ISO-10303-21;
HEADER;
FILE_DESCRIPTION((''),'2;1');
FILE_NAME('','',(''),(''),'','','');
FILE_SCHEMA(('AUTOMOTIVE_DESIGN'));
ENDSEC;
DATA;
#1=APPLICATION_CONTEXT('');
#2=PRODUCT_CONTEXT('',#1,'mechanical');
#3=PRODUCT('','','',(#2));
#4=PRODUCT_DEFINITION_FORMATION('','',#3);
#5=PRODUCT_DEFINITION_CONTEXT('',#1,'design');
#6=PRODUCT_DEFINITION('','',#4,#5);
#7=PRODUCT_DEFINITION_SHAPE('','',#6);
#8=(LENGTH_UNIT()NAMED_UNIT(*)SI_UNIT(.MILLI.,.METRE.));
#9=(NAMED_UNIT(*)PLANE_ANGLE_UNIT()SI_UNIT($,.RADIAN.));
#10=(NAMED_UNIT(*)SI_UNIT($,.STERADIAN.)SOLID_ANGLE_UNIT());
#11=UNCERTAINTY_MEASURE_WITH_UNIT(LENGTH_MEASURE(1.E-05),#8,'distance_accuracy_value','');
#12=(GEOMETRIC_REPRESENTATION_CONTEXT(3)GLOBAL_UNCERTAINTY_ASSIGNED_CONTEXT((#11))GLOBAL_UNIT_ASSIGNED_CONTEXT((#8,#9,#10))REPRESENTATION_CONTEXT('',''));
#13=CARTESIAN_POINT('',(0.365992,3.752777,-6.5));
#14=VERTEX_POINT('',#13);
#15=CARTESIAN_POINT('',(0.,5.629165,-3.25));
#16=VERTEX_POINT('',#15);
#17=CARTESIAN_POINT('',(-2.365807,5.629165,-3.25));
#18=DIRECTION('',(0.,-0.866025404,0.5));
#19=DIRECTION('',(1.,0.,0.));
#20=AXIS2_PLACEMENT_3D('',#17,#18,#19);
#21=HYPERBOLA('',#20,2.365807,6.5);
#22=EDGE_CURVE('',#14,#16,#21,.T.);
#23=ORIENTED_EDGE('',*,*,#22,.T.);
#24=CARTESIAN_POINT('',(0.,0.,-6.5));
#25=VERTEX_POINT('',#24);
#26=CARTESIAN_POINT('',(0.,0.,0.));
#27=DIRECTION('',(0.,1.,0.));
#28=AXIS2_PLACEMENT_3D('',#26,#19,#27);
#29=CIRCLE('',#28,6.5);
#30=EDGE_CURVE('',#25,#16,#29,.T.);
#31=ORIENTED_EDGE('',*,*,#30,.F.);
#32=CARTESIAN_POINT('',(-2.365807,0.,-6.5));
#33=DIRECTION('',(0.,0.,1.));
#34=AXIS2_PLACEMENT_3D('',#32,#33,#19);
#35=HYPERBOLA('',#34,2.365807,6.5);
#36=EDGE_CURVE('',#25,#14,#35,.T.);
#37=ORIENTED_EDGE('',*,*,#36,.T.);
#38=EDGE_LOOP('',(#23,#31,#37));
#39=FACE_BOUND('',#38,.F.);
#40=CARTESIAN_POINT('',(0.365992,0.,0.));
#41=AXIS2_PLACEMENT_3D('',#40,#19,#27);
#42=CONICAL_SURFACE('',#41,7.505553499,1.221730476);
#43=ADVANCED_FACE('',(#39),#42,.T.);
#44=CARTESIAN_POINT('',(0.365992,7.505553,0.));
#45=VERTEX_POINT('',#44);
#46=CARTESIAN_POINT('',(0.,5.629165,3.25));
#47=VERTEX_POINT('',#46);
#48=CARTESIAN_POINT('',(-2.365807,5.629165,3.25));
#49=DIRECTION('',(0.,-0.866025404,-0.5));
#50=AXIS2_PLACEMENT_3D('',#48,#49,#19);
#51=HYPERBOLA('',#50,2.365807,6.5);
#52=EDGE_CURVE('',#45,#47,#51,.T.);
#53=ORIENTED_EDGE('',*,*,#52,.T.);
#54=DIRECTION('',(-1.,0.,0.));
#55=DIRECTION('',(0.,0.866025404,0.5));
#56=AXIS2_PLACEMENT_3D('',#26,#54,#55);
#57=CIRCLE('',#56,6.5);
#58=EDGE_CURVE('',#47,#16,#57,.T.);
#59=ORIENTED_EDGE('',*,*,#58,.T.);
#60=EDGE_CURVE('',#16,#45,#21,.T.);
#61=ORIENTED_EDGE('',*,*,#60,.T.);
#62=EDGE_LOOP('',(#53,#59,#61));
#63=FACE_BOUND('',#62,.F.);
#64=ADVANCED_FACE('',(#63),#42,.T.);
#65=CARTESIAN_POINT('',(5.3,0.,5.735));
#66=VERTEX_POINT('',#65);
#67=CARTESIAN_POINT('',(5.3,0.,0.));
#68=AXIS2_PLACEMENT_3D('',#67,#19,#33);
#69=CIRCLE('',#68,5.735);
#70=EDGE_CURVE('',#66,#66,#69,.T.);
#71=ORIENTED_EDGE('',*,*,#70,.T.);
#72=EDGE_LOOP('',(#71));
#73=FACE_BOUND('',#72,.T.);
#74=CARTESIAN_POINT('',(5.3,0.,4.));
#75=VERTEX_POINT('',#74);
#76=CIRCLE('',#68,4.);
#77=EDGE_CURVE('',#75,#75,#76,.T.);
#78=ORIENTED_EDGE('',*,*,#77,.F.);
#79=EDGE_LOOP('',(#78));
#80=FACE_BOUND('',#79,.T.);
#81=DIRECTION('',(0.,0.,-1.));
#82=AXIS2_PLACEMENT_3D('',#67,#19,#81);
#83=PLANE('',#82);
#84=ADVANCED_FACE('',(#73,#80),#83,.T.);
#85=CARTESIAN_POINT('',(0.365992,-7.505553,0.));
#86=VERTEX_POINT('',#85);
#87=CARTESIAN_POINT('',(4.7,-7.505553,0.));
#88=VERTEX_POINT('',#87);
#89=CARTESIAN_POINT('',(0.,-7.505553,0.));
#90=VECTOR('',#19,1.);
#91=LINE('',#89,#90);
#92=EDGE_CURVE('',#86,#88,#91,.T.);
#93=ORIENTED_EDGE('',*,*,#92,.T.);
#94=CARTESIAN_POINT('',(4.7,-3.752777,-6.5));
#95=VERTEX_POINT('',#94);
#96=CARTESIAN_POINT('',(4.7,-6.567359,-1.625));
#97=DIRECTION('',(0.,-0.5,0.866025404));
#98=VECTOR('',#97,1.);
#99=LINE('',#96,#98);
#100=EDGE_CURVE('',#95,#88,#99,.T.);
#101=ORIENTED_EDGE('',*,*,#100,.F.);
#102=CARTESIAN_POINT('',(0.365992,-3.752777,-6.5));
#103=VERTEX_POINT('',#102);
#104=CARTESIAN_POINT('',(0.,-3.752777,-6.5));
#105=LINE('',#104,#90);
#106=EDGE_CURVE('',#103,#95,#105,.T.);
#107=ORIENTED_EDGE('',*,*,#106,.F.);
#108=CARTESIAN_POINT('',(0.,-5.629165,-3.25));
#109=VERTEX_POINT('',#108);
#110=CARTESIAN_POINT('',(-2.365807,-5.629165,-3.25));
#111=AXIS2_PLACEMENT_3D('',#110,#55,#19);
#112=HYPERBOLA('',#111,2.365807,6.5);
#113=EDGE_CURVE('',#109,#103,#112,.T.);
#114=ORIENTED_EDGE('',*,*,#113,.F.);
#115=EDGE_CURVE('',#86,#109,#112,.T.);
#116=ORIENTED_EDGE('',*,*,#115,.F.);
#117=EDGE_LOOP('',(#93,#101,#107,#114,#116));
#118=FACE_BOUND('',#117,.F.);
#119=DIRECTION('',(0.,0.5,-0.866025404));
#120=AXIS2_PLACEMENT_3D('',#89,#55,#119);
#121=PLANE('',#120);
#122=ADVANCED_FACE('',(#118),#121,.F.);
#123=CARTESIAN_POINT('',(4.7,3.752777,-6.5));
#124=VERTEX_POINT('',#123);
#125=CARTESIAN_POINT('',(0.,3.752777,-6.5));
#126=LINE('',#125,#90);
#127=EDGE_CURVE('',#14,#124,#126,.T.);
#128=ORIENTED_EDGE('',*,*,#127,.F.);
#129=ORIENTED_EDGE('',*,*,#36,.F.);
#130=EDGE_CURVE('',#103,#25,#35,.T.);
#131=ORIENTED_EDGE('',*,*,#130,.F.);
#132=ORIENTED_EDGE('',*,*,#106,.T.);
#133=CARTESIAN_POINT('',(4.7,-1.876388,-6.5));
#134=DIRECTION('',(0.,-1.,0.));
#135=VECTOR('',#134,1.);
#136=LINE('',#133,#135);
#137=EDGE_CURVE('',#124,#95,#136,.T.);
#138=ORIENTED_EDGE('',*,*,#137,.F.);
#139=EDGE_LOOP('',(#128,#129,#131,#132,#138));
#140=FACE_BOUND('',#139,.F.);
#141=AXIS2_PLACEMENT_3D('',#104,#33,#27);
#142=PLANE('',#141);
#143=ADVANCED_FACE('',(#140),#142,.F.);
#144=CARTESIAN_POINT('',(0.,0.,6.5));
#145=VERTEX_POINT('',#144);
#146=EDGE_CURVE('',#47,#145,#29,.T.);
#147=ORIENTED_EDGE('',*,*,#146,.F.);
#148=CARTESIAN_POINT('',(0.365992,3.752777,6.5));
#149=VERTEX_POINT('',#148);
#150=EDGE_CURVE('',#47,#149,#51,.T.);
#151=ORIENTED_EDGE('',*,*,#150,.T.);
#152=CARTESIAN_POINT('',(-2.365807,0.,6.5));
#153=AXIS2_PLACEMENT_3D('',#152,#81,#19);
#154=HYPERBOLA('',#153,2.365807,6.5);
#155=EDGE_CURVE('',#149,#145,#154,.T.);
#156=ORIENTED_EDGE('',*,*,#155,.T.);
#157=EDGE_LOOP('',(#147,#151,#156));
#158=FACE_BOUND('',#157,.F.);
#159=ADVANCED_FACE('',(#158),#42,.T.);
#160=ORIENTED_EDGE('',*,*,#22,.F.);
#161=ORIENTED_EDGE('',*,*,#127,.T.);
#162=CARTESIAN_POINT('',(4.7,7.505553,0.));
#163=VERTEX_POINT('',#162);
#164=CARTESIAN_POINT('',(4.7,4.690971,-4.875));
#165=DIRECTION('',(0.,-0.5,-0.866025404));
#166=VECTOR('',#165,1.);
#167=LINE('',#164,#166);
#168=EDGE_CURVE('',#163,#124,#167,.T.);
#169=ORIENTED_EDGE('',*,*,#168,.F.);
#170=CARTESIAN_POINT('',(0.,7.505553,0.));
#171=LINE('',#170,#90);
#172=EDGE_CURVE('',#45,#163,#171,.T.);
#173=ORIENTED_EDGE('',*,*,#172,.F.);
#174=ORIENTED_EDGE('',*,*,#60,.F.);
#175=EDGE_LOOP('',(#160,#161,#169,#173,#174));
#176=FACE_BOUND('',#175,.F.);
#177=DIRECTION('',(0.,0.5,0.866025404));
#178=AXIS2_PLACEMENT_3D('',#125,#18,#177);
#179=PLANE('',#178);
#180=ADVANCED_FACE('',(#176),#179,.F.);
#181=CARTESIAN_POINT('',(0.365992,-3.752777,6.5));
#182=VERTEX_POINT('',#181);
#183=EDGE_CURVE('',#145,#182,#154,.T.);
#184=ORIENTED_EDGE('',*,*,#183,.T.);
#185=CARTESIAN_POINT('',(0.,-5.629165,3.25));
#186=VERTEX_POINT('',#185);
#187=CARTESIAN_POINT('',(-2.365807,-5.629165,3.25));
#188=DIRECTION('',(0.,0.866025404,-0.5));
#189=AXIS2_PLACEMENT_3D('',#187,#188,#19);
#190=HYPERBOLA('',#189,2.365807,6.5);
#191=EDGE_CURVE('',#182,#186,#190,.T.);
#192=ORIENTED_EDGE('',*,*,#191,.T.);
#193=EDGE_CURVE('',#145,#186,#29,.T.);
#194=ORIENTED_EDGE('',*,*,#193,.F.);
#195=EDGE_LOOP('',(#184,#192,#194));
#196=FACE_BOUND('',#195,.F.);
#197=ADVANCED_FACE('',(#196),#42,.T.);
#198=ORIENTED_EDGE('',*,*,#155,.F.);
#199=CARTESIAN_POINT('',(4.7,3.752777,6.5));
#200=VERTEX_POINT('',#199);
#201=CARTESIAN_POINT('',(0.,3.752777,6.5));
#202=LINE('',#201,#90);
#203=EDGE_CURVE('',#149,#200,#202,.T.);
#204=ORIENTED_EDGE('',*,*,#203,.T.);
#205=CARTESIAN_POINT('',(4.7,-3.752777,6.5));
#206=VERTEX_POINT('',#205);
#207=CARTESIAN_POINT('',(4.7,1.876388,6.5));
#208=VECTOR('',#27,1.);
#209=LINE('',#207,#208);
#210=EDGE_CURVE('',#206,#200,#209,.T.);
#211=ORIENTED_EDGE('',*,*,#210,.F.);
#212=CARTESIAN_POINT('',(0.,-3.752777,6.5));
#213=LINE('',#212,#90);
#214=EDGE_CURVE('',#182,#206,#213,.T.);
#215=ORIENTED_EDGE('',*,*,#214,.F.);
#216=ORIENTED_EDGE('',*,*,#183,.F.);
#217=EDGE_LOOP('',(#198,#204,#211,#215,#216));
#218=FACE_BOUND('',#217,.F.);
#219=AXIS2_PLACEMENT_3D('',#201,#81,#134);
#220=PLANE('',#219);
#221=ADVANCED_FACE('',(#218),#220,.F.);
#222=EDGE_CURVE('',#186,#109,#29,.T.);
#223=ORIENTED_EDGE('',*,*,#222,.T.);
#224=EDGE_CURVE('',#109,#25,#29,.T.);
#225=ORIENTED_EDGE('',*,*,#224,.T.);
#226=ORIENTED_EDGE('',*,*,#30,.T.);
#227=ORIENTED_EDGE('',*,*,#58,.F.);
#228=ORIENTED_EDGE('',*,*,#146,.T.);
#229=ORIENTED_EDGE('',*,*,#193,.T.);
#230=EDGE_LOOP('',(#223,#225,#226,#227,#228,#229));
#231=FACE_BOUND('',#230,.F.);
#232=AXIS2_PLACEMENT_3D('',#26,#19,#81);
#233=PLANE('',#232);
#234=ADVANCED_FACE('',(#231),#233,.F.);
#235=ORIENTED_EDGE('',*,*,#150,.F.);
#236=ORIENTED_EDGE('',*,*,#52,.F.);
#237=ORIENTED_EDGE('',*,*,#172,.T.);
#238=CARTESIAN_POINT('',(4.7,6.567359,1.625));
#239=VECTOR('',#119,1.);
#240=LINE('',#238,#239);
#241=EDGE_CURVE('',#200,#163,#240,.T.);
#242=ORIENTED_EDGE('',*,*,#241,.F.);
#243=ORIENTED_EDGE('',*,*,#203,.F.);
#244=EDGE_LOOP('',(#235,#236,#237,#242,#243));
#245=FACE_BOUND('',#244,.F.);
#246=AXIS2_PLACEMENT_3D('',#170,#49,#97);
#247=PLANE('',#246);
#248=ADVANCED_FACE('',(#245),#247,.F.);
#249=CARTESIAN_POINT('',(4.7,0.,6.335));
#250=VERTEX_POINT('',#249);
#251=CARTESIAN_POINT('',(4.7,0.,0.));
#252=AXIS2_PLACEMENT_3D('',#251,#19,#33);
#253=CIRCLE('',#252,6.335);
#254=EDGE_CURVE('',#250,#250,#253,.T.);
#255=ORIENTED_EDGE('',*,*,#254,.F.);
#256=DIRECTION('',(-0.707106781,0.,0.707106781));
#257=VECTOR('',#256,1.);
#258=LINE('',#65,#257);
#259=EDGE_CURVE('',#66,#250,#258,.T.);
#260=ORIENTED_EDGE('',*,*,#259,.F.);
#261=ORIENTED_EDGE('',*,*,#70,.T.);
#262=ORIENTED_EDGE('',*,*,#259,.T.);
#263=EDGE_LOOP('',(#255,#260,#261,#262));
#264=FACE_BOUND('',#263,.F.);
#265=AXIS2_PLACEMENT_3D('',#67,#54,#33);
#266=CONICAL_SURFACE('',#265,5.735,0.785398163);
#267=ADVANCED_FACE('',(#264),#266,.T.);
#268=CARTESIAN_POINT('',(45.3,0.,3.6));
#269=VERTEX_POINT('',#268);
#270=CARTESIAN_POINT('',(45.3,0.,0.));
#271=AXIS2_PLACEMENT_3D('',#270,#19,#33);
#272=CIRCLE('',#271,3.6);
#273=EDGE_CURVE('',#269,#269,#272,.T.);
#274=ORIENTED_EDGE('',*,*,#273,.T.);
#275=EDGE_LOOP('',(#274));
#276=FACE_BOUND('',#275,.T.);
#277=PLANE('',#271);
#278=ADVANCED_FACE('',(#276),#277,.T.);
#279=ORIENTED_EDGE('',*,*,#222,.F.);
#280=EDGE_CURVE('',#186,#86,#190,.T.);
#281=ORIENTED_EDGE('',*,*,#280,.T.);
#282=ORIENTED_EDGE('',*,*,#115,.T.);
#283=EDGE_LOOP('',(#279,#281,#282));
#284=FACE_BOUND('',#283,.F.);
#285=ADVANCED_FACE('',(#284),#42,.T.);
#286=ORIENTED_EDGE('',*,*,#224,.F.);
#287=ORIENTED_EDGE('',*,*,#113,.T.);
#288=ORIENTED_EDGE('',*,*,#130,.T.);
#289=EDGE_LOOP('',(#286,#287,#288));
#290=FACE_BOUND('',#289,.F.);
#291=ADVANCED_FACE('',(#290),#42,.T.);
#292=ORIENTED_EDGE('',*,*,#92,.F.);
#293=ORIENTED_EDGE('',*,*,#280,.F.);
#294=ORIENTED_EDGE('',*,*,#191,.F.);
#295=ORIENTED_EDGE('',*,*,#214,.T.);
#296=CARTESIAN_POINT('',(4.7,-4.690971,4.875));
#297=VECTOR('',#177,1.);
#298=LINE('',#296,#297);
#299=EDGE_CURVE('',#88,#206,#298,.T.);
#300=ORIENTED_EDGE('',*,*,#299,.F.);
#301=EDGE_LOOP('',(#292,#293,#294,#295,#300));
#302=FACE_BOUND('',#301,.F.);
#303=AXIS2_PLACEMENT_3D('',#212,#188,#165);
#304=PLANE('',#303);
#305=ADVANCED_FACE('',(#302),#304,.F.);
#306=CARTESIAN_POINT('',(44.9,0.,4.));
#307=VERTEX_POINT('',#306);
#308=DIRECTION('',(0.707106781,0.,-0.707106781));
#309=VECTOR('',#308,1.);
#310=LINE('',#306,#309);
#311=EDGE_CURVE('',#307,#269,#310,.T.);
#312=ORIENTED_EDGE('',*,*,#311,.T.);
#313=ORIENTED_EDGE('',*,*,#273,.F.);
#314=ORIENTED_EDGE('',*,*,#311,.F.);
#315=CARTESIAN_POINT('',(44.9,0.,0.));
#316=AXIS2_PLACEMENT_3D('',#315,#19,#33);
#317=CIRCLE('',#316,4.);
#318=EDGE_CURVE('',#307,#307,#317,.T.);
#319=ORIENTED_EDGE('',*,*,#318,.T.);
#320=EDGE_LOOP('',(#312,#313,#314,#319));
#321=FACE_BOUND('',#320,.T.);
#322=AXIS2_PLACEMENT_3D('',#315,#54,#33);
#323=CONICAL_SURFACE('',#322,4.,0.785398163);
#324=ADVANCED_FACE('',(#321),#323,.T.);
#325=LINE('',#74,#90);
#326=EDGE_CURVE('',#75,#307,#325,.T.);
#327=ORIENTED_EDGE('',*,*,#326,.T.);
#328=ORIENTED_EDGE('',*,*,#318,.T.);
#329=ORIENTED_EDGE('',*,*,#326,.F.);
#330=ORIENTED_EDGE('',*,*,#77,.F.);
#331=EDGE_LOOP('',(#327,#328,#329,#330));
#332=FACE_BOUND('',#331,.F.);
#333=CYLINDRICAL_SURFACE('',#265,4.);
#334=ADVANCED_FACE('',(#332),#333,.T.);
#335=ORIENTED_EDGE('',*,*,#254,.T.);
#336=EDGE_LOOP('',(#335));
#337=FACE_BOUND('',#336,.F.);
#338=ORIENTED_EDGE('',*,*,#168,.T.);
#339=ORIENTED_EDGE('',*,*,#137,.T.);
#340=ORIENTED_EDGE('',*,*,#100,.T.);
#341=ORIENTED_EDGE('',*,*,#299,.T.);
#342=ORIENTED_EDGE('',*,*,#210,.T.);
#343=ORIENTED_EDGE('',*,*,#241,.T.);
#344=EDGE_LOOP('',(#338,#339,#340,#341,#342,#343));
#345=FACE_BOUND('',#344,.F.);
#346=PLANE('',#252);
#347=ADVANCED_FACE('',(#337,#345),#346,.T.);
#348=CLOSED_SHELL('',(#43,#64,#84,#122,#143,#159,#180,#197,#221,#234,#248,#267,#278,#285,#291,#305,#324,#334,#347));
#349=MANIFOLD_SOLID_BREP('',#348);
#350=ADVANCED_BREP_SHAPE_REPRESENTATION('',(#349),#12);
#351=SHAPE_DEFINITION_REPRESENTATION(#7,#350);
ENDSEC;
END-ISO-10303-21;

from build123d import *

# Parameters (mm, degrees)
BASEHEAD_DEPTH = 5.3
SKETCH5_R      = 4
BASEBODY_DEPTH = 40
CHAMFER1_SIZE  = 0.4


with BuildPart() as part:
    # Sketch2 → BaseHead (new body)
    with BuildSketch(Plane(origin=(0, 0, 0), x_dir=(0, 0, -1), z_dir=(1, 0, 0))):
        Polygon((0, -7.505553499), (6.5, -3.75277675), (6.5, 3.75277675), (0, 7.505553499), (-6.5, 3.75277675), (-6.5, -3.75277675), align=None)
    extrude(amount=BASEHEAD_DEPTH)

    # Sketch3 → BearingFace (revolve, cut)
    with BuildSketch(Plane.XY, mode=Mode.PRIVATE) as bearingface_sk:
        Polygon((5.3, 7.505553499), (5.3, 5.735), (4.7, 6.335), (4.7, 7.505553499), align=None)
    revolve(bearingface_sk.sketch.rotate(Axis((-0.957090588, 0, 0), (1, 0, 0)), 90), axis=Axis((-0.957090588, 0, 0), (1, 0, 0)), mode=Mode.SUBTRACT)

    # Sketch4 → HeadChamfer (revolve, cut)
    with BuildSketch(Plane.XY):
        Polygon((0, 7.505553499), (0.365991543, 7.505553499), (0, 6.5), align=None)
    revolve(axis=Axis((-0.493528746, 0, 0), (1, 0, 0)), mode=Mode.SUBTRACT)

    # Sketch5 → BaseBody (add)
    with BuildSketch(Plane(origin=(5.3, 0, 0), x_dir=(0, 0, -1), z_dir=(1, 0, 0))):
        with Locations(Location((0, 0, 0), (0, 0, 180))):
            Circle(SKETCH5_R)
    extrude(amount=BASEBODY_DEPTH)

    # Chamfer1
    chamfer1_edges = [part.edges().sort_by_distance(p)[0] for p in [
        (45.3, 0, -4),
    ]]
    chamfer(chamfer1_edges, length=CHAMFER1_SIZE)


solid = part.part
